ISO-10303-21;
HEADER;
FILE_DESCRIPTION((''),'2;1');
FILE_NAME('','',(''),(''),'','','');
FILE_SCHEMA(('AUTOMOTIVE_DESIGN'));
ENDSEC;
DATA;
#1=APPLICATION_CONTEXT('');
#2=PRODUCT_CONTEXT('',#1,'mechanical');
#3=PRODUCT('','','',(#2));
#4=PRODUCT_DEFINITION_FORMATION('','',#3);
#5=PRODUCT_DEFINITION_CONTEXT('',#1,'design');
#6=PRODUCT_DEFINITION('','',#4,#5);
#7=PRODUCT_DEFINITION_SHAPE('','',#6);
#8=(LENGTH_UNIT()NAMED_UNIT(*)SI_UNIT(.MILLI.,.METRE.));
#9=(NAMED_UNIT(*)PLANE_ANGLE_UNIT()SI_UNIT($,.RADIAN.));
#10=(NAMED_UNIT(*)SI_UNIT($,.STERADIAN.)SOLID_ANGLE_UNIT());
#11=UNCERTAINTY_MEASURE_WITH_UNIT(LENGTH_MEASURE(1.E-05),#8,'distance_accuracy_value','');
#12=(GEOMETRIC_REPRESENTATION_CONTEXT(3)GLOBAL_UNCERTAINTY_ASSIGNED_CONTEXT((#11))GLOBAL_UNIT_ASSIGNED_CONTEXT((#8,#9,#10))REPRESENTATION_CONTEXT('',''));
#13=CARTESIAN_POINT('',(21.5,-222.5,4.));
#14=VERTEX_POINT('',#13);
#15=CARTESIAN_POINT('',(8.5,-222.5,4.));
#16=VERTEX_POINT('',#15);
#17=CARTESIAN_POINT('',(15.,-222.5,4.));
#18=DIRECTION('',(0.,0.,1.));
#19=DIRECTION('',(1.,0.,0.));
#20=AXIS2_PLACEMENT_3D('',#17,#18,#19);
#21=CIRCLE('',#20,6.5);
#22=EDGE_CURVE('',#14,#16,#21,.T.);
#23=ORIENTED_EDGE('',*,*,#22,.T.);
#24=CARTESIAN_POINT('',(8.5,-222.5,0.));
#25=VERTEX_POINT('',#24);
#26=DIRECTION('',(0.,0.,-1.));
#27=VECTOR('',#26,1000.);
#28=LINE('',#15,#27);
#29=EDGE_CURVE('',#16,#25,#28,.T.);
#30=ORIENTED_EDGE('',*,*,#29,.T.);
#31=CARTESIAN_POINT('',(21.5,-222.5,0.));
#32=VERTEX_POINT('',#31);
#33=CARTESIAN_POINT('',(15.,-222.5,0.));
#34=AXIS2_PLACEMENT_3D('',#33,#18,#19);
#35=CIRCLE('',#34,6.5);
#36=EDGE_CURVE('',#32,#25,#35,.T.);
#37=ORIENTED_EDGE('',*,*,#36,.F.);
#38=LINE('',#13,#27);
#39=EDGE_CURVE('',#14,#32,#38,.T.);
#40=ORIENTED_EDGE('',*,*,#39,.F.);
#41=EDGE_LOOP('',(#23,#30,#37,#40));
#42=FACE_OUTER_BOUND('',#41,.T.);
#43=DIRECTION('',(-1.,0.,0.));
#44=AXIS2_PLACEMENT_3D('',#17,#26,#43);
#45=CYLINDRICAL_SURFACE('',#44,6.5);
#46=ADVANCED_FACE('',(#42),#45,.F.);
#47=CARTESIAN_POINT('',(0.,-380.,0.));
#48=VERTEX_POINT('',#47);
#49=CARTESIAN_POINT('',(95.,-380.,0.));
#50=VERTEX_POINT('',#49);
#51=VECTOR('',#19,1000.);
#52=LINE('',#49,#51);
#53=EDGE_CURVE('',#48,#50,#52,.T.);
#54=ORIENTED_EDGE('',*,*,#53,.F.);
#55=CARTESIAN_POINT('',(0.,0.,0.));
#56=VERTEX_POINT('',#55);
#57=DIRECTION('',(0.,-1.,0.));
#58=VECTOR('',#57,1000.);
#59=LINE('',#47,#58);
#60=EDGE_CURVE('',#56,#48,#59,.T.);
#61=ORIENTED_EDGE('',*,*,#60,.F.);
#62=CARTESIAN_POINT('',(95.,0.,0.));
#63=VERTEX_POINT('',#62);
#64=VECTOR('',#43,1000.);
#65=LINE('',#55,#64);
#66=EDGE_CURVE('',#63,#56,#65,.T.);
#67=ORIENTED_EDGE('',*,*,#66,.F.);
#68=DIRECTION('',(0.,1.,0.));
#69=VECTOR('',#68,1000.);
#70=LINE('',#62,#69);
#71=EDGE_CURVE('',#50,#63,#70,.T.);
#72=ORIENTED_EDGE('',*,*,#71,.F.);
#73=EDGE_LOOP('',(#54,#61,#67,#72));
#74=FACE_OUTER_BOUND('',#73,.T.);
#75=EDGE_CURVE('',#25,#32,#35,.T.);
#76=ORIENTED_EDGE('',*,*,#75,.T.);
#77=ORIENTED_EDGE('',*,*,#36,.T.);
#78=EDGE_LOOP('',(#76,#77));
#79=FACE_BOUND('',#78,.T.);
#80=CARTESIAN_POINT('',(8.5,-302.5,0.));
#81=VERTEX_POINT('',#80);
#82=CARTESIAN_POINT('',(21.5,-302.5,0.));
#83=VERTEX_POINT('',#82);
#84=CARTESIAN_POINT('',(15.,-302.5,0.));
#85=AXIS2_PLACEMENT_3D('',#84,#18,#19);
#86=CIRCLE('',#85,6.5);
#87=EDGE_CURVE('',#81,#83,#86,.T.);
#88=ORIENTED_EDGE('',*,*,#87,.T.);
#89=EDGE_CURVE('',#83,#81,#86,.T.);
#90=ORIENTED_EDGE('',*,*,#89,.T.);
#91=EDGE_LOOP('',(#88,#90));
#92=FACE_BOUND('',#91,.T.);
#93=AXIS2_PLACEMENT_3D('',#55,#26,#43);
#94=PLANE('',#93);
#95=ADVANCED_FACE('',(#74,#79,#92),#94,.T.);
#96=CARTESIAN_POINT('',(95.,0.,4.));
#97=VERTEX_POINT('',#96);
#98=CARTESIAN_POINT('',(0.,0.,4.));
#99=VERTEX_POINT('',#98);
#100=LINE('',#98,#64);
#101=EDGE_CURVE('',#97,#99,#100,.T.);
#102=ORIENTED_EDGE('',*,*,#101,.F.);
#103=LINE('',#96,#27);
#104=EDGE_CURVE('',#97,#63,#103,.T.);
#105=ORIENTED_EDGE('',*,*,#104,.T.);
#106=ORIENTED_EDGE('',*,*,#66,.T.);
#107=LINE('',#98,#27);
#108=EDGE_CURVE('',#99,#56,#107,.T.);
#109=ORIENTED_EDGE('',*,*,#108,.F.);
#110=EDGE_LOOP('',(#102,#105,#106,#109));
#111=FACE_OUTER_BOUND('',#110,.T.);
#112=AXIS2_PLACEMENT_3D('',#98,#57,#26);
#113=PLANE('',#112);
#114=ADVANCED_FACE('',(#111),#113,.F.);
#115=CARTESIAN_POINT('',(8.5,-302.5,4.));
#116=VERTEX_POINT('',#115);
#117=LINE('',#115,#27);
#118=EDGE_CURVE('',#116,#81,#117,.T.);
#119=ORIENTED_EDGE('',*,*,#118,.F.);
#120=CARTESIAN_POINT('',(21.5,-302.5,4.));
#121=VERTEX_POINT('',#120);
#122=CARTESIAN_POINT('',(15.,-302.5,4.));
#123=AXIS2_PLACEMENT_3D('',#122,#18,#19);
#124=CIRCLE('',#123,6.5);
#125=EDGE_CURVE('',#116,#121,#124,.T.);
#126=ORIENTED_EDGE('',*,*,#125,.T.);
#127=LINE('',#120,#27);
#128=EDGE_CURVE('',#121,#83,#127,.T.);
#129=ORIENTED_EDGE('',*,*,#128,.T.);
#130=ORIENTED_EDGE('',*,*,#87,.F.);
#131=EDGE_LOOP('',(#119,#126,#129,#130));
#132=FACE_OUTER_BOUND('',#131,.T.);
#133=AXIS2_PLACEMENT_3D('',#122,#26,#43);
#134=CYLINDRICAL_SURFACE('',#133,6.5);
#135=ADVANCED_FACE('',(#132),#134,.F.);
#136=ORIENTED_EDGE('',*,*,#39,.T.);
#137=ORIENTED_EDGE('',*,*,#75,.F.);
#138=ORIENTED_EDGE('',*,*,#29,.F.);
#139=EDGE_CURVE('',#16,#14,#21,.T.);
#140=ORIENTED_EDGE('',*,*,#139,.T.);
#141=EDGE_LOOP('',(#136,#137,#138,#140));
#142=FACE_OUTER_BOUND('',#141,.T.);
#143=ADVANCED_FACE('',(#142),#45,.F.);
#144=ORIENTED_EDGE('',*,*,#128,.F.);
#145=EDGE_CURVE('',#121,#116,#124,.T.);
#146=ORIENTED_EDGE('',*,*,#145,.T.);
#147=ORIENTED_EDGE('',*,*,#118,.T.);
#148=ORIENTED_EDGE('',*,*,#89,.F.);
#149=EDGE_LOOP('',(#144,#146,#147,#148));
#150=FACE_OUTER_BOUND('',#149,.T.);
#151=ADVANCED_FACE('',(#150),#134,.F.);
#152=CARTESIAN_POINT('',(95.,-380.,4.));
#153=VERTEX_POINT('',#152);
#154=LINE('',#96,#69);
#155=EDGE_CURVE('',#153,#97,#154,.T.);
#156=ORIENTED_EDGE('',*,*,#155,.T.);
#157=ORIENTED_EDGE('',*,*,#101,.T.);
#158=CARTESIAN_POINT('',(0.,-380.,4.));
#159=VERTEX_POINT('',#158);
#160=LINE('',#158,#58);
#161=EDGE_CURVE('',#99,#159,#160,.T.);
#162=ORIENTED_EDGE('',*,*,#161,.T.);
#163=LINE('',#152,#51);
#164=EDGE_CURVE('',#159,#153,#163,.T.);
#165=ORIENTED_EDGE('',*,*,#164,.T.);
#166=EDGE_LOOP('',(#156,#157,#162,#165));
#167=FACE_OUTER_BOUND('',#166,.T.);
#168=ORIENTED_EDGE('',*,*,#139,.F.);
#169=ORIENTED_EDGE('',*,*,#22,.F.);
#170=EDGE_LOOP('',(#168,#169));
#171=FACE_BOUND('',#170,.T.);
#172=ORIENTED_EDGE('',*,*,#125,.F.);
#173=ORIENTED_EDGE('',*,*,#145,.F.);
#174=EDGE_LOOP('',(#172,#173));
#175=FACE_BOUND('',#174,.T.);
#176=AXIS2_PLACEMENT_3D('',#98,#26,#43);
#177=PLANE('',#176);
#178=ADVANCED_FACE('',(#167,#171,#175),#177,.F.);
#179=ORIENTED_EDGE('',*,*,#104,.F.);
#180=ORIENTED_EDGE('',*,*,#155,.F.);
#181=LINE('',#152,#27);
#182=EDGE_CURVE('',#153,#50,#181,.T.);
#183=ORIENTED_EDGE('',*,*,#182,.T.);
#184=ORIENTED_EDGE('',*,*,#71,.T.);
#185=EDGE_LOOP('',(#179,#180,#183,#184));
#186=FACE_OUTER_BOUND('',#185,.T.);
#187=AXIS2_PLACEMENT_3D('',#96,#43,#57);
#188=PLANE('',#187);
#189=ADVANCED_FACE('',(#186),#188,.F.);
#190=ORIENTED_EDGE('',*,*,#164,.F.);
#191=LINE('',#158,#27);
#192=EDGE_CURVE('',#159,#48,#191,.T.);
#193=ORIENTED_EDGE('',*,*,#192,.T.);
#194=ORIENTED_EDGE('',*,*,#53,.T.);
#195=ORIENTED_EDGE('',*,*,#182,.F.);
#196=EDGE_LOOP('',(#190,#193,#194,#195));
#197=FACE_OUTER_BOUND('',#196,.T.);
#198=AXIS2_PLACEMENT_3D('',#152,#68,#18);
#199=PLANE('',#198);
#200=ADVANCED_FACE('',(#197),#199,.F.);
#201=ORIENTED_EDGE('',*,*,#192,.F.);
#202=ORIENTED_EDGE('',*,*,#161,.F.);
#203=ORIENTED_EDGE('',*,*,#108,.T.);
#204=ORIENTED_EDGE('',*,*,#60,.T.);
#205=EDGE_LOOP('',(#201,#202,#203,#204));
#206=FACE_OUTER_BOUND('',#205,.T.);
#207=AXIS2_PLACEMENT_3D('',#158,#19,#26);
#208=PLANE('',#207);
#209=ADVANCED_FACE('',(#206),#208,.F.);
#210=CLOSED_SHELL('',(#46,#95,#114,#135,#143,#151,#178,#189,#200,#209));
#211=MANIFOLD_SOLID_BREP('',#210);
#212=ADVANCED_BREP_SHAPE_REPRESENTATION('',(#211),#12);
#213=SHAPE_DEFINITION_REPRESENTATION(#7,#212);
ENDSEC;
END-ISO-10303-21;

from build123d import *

# Parameters (mm, degrees)
SKETCH_1_W      = 95
SKETCH_1_H      = 380
SKETCH_1_R      = 6.5
EXTRUDE_2_DEPTH = 4


with BuildPart() as part:
    # 草图1 → 凸台-拉伸2 (new body)
    with BuildSketch(Plane.XY):
        with Locations((47.5, -190)):
            Rectangle(SKETCH_1_W, SKETCH_1_H)
        with Locations((15, -302.5)):
            Circle(SKETCH_1_R, mode=Mode.SUBTRACT)
        with Locations((15, -222.5)):
            Circle(SKETCH_1_R, mode=Mode.SUBTRACT)
    extrude(amount=EXTRUDE_2_DEPTH)


solid = part.part
